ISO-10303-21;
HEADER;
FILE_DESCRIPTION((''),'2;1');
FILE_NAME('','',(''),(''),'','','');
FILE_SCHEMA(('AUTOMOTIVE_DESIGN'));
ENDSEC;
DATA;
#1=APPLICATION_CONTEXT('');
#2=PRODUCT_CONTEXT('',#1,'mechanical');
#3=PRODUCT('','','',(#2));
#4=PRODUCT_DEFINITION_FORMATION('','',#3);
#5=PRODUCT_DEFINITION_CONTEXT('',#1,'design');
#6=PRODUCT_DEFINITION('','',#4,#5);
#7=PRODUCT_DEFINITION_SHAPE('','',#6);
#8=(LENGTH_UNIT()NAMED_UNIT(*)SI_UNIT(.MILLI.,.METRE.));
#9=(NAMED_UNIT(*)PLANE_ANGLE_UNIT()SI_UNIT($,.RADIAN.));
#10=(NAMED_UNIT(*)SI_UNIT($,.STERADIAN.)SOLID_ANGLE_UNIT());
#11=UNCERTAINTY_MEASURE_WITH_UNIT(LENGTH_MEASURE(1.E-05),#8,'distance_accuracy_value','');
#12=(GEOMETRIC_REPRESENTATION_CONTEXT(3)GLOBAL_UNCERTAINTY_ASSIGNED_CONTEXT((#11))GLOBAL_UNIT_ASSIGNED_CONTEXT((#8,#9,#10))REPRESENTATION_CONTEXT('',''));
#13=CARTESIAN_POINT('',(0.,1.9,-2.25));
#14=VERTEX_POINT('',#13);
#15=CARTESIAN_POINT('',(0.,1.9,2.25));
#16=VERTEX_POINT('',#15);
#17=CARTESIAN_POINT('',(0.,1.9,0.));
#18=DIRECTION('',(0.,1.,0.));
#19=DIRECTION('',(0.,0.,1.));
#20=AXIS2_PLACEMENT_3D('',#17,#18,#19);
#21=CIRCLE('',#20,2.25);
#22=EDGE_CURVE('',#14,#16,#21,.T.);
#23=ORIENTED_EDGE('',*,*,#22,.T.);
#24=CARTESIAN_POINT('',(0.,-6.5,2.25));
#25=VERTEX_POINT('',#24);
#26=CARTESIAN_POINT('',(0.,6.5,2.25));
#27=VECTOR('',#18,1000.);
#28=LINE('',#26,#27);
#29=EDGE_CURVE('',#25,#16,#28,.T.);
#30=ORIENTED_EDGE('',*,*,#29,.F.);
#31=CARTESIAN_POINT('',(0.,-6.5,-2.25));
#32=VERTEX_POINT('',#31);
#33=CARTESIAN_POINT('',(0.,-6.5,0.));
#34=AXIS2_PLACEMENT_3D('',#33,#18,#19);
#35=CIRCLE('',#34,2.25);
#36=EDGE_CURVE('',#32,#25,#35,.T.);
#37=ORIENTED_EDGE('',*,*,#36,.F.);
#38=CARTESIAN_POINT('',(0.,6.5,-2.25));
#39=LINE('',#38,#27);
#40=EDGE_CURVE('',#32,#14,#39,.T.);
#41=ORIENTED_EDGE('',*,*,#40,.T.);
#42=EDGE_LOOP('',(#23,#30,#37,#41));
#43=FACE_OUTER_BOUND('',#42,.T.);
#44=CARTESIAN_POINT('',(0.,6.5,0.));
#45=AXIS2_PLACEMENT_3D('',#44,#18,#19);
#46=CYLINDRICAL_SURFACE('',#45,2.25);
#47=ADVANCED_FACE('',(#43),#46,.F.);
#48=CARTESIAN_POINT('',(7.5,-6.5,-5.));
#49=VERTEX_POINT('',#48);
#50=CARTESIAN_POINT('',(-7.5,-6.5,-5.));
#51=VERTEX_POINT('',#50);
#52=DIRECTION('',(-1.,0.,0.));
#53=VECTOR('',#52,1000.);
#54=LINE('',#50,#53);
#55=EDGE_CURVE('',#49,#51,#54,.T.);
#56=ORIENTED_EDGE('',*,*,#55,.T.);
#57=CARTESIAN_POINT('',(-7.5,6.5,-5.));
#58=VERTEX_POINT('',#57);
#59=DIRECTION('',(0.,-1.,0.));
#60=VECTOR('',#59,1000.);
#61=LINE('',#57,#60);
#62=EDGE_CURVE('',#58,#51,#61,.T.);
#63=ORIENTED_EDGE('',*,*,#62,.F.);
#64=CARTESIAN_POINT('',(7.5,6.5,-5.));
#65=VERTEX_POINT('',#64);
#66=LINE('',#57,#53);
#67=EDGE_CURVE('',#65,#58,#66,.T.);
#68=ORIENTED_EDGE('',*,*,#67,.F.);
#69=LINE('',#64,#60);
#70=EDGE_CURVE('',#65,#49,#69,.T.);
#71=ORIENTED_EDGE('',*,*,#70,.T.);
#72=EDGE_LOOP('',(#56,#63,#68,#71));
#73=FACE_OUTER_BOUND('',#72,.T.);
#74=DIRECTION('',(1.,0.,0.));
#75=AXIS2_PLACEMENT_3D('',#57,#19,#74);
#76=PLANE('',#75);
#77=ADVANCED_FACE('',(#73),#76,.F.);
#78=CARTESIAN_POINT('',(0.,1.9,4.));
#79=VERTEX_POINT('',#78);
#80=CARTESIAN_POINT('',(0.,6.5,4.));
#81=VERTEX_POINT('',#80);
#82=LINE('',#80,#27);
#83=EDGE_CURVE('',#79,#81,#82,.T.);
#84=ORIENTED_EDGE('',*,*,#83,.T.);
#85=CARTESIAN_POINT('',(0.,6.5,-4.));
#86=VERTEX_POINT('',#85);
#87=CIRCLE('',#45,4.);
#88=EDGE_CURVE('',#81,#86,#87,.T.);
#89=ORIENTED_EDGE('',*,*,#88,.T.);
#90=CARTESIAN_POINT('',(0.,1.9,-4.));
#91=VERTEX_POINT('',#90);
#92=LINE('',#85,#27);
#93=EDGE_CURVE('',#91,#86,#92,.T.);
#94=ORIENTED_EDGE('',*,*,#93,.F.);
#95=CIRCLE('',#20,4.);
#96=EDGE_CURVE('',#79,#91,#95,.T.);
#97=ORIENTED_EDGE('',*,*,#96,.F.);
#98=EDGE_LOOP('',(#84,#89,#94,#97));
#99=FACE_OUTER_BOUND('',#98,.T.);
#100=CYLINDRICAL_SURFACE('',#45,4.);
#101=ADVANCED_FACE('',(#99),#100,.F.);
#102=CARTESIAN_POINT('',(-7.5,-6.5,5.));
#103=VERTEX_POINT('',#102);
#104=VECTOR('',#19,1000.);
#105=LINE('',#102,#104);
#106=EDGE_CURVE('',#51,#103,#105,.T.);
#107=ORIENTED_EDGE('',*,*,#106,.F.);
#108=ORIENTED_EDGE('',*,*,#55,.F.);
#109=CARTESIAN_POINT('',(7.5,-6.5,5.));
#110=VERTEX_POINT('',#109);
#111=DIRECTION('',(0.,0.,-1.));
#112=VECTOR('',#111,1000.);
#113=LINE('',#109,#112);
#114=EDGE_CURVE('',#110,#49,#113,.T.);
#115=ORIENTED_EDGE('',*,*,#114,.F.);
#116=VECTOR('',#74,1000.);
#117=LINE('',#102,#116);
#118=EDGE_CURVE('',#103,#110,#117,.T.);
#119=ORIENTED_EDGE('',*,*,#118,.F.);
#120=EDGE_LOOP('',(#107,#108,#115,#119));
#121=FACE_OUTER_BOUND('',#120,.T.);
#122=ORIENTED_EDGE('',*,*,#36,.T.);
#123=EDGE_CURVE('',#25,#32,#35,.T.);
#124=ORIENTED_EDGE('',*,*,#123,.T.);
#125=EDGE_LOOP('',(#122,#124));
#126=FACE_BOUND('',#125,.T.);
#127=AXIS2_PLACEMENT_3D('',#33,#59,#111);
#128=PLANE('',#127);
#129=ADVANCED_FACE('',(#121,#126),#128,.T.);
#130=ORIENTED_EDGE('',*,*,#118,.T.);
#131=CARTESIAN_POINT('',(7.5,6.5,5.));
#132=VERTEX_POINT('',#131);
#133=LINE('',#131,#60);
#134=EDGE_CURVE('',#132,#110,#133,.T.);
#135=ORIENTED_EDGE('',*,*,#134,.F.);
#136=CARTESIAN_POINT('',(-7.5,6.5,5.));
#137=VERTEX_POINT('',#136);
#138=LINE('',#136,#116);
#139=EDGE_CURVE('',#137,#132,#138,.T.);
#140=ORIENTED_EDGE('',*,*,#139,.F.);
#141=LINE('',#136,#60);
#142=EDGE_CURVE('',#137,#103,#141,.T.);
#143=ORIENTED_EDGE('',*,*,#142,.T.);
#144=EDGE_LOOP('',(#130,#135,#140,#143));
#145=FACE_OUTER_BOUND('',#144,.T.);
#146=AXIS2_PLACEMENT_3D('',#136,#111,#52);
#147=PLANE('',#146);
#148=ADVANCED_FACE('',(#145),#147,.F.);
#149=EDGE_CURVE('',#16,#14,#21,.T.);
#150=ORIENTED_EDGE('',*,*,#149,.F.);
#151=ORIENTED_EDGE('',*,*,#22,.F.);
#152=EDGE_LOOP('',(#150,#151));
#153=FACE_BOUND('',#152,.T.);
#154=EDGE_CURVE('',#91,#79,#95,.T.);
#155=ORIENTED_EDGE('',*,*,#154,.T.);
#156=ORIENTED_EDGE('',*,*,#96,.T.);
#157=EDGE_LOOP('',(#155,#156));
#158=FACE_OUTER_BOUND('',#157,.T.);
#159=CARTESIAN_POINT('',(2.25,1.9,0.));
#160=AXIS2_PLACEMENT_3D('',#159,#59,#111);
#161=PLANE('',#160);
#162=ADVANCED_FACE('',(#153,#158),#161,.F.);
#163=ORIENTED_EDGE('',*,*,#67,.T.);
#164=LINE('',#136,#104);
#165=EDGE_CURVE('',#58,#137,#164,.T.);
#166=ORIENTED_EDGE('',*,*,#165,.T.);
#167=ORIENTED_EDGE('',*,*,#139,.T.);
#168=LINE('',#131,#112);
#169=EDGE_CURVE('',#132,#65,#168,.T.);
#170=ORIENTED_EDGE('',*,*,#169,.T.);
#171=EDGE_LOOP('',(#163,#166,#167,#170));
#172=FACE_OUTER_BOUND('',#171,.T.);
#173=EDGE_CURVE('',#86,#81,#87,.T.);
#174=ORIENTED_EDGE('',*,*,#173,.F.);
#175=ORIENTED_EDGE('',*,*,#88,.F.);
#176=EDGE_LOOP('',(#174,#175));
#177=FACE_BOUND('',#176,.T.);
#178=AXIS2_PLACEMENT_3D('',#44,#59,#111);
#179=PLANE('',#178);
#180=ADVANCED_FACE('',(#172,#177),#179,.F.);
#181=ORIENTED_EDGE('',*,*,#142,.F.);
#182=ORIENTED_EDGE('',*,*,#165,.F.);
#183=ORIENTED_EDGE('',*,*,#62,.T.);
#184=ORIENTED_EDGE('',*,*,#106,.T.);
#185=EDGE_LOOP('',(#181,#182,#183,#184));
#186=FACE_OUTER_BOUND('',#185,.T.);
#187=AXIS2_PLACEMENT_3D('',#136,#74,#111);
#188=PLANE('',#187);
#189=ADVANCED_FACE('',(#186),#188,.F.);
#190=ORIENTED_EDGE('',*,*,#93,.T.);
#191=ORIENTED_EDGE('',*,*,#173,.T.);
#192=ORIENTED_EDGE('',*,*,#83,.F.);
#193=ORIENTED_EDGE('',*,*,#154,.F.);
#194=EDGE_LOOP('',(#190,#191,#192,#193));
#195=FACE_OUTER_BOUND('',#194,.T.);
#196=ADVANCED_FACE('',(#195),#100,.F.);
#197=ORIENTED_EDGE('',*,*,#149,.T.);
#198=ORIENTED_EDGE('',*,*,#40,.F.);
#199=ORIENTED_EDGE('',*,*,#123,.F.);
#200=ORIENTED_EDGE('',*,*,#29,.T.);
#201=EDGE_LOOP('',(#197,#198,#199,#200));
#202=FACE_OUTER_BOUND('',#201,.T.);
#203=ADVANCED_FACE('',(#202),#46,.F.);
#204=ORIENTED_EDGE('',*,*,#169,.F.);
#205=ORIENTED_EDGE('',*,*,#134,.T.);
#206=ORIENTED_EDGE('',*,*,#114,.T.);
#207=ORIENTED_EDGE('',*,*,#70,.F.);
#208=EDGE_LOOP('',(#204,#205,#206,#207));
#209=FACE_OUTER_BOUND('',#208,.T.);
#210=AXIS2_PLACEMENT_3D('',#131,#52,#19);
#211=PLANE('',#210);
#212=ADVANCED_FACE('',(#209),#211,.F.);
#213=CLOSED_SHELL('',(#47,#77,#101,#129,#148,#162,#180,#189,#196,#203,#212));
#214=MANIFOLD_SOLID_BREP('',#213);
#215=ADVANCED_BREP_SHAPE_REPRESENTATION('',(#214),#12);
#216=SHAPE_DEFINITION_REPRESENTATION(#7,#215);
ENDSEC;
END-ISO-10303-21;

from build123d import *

# Parameters (mm, degrees)
SKETCH_1_W                = 15
SKETCH_1_H                = 10
EXTRUDE_1_DEPTH           = 6.5
HOLE_WIZARD_1_D           = 4.5
HOLE_WIZARD_1_CBORE_D     = 8
HOLE_WIZARD_1_CBORE_DEPTH = 4.6


with BuildPart() as part:
    # 草图1 → 凸台-拉伸1 (new, symmetric)
    with BuildSketch(Plane(origin=(0, 0, 0), x_dir=(1, 0, 0), z_dir=(0, 1, 0))):
        Rectangle(SKETCH_1_W, SKETCH_1_H)
    extrude(amount=EXTRUDE_1_DEPTH, both=True)

    # 打孔尺寸(%根据)内六角圆柱头螺钉的类型1 (through all)
    with Locations(Plane(origin=(0, 6.5, 0), x_dir=(1, 0, 0), z_dir=(0, 1, 0))):
        with Locations((0, 0)):
            CounterBoreHole(HOLE_WIZARD_1_D / 2, HOLE_WIZARD_1_CBORE_D / 2, HOLE_WIZARD_1_CBORE_DEPTH)


solid = part.part
